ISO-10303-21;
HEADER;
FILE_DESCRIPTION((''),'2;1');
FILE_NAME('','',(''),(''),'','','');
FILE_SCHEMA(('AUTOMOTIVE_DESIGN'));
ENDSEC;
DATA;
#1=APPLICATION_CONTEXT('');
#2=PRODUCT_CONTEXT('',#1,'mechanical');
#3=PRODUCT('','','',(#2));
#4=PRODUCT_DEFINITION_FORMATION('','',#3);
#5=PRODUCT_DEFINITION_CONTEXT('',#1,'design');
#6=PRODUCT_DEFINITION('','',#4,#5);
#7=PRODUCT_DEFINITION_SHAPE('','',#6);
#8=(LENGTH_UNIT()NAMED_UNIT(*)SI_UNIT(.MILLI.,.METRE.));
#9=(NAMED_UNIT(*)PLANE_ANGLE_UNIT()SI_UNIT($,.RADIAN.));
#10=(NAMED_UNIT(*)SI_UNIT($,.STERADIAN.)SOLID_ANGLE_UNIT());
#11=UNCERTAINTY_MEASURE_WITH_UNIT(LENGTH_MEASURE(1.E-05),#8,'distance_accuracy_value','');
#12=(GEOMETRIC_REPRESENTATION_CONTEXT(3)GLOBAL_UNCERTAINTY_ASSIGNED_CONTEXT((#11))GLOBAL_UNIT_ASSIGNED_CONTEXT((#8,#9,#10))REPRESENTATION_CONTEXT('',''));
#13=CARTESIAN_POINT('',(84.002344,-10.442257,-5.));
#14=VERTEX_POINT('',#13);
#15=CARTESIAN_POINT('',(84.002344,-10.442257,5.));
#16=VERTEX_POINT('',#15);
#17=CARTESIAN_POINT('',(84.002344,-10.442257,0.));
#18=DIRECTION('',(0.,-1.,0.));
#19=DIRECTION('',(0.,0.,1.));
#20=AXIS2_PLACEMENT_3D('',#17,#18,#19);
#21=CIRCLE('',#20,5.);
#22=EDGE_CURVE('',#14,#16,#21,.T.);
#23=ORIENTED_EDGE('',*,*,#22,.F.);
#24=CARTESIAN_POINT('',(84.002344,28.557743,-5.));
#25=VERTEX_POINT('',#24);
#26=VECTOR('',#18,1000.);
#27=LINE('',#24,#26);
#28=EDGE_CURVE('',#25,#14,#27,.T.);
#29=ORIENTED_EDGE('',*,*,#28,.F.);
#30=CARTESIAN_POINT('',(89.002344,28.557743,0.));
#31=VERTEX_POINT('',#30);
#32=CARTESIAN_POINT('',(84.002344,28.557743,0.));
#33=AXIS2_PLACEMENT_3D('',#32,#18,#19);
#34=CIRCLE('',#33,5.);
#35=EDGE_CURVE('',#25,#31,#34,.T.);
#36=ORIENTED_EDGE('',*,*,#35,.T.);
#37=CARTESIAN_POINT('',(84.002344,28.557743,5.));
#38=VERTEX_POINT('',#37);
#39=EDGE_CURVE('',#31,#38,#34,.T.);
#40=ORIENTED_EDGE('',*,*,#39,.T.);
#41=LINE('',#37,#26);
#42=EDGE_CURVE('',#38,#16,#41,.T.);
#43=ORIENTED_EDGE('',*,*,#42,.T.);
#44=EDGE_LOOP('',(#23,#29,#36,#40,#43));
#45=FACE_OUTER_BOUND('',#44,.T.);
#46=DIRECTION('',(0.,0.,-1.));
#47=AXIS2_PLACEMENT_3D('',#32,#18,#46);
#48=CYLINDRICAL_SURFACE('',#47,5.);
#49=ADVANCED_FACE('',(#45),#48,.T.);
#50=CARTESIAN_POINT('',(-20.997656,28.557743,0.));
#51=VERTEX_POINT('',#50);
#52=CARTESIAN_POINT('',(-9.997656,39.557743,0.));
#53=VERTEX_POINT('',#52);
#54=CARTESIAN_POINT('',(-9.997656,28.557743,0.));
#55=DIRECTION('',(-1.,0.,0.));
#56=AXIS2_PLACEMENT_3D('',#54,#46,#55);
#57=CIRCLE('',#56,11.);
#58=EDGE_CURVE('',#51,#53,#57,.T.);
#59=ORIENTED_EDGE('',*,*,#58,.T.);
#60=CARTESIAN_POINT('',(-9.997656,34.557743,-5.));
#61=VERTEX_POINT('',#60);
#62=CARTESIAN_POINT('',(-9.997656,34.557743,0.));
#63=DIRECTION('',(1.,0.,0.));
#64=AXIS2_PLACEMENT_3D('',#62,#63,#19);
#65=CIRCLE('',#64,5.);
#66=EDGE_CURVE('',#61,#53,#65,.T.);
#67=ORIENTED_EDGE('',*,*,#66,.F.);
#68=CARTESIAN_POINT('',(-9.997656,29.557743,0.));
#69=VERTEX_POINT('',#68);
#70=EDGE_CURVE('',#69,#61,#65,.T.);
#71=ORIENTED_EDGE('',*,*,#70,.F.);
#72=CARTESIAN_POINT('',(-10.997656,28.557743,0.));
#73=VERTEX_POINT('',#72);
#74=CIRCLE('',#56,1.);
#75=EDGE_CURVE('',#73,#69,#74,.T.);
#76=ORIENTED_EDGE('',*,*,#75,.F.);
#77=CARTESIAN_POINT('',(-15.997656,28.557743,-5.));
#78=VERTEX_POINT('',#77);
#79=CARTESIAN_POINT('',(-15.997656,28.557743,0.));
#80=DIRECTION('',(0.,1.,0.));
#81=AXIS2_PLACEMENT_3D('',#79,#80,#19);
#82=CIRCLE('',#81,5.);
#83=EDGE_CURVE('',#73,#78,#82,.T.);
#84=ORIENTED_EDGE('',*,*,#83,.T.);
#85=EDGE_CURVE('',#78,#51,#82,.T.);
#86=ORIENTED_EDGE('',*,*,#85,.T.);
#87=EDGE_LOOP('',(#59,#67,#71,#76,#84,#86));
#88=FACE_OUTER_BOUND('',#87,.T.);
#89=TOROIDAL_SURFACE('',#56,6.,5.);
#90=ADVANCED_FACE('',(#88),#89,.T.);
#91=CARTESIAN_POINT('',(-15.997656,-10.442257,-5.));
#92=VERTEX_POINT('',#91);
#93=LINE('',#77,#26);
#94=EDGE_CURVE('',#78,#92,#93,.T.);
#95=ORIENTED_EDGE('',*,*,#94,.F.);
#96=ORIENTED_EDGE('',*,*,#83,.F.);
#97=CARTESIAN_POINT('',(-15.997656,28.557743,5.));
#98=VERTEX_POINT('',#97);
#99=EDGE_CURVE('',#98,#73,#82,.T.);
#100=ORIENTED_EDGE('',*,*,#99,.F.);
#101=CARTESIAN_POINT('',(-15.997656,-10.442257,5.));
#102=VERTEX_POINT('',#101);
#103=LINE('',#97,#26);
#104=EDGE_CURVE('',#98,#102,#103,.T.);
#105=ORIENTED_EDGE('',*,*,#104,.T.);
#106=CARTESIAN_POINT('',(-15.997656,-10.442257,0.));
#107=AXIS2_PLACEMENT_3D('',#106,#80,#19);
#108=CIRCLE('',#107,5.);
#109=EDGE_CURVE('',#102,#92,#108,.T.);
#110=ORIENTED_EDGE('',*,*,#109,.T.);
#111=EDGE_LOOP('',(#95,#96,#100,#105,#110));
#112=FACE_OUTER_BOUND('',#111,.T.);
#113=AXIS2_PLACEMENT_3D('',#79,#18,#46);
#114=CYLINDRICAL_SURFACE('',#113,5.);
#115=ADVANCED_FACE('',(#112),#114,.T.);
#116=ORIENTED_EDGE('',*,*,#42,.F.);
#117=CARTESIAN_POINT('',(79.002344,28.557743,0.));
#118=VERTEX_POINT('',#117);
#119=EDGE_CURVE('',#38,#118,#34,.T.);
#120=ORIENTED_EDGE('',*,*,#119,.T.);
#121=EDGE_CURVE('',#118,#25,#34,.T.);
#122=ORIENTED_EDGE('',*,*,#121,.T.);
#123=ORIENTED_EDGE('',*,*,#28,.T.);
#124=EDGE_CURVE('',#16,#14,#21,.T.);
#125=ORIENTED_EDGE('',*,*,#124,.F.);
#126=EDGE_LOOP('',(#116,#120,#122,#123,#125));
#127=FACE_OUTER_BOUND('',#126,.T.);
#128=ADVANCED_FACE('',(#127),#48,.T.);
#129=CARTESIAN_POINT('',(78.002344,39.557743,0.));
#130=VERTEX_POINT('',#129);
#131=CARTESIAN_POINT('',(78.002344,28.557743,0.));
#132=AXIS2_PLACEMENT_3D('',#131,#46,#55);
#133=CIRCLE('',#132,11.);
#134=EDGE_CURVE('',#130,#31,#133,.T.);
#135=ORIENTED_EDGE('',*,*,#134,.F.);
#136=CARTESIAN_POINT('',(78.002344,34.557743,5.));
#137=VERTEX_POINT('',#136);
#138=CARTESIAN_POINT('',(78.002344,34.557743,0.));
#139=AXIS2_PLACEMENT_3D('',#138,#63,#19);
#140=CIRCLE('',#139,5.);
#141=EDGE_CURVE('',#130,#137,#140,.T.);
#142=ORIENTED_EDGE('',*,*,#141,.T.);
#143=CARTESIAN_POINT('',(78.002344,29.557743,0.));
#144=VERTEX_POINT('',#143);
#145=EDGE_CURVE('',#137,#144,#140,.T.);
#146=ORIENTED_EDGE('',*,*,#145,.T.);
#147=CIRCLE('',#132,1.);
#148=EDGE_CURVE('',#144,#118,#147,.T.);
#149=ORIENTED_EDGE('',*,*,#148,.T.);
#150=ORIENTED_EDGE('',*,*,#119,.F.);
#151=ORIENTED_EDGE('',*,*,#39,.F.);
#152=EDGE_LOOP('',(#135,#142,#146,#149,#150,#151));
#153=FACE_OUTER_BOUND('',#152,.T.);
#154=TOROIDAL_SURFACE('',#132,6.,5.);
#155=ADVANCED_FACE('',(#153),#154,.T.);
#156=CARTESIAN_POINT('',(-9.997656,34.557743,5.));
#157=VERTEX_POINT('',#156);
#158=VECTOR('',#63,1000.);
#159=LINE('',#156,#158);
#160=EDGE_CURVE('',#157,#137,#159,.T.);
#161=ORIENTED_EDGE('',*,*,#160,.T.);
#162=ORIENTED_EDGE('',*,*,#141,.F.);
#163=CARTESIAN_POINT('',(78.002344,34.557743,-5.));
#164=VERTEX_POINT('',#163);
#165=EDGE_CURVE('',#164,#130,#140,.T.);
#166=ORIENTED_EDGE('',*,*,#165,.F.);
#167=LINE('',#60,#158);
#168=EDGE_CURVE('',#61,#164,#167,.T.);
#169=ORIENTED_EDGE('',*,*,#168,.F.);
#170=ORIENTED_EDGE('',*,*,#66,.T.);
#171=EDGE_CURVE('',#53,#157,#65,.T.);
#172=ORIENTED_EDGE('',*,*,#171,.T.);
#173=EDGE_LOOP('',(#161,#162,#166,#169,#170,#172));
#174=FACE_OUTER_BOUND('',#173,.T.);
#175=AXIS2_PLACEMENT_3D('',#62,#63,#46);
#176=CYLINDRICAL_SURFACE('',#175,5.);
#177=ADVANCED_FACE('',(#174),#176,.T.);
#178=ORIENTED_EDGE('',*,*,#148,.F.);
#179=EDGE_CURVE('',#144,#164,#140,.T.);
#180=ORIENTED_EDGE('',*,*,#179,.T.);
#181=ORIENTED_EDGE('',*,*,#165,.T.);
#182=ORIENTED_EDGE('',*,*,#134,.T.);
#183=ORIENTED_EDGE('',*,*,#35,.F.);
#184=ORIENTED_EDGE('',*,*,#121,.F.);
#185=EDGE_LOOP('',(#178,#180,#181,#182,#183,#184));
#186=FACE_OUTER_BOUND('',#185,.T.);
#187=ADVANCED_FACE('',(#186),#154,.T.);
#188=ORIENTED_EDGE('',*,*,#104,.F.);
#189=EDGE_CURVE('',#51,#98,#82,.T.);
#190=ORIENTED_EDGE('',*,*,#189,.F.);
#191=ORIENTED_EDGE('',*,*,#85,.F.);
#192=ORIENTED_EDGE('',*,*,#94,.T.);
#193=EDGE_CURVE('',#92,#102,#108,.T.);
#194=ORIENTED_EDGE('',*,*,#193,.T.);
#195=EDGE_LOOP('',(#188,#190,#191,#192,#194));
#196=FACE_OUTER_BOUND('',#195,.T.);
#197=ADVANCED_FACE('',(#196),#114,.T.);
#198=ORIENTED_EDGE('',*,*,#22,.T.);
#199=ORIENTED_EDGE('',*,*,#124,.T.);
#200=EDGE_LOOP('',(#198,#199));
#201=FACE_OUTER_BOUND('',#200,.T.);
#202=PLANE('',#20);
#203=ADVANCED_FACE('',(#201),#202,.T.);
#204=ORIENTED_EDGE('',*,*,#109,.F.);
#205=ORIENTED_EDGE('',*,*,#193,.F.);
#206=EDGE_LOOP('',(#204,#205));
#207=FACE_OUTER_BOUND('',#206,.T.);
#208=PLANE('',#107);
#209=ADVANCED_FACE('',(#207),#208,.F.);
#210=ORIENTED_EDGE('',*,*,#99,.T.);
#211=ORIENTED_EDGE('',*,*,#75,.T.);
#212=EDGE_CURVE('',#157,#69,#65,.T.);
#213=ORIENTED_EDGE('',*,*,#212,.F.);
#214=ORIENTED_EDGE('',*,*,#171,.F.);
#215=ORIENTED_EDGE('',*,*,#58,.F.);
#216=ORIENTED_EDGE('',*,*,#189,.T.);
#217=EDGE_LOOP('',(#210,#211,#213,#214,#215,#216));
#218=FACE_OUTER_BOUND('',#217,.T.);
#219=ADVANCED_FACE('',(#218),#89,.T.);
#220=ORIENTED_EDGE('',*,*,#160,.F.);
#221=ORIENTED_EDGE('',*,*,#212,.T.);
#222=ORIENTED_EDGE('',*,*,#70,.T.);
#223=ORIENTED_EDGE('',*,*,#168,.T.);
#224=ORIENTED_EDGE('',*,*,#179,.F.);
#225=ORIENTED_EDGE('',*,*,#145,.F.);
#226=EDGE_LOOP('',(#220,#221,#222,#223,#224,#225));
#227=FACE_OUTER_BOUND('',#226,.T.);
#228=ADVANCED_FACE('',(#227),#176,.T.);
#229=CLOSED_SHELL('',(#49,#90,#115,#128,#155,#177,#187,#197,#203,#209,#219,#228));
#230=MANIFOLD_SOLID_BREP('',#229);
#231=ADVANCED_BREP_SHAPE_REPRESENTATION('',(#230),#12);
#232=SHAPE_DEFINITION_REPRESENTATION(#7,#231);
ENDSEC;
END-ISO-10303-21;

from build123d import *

# Parameters (mm, degrees)
SKETCH2_R = 5


with BuildPart() as part:
    # Sweep1: sweep along a path in Sketch1
    with BuildLine(Plane.XY) as sweep1_path:
        Line((-15.997655985, -10.44225726), (-15.997655985, 28.55774274))
        ThreePointArc((-15.997655985, 28.55774274), (-14.240296673, 32.800383427), (-9.997655985, 34.55774274))
        Line((-9.997655985, 34.55774274), (78.002344015, 34.55774274))
        ThreePointArc((78.002344015, 34.55774274), (82.244984702, 32.800383427), (84.002344015, 28.55774274))
        Line((84.002344015, 28.55774274), (84.002344015, -10.44225726))
    # Sketch2 → Sweep1 (sweep)
    with BuildSketch(Plane(origin=(-15.997655985, -10.44225726, 0), x_dir=(-1, 0, 0), z_dir=(0, 1, 0))):
        Circle(SKETCH2_R)
    sweep(path=sweep1_path.line)


solid = part.part
